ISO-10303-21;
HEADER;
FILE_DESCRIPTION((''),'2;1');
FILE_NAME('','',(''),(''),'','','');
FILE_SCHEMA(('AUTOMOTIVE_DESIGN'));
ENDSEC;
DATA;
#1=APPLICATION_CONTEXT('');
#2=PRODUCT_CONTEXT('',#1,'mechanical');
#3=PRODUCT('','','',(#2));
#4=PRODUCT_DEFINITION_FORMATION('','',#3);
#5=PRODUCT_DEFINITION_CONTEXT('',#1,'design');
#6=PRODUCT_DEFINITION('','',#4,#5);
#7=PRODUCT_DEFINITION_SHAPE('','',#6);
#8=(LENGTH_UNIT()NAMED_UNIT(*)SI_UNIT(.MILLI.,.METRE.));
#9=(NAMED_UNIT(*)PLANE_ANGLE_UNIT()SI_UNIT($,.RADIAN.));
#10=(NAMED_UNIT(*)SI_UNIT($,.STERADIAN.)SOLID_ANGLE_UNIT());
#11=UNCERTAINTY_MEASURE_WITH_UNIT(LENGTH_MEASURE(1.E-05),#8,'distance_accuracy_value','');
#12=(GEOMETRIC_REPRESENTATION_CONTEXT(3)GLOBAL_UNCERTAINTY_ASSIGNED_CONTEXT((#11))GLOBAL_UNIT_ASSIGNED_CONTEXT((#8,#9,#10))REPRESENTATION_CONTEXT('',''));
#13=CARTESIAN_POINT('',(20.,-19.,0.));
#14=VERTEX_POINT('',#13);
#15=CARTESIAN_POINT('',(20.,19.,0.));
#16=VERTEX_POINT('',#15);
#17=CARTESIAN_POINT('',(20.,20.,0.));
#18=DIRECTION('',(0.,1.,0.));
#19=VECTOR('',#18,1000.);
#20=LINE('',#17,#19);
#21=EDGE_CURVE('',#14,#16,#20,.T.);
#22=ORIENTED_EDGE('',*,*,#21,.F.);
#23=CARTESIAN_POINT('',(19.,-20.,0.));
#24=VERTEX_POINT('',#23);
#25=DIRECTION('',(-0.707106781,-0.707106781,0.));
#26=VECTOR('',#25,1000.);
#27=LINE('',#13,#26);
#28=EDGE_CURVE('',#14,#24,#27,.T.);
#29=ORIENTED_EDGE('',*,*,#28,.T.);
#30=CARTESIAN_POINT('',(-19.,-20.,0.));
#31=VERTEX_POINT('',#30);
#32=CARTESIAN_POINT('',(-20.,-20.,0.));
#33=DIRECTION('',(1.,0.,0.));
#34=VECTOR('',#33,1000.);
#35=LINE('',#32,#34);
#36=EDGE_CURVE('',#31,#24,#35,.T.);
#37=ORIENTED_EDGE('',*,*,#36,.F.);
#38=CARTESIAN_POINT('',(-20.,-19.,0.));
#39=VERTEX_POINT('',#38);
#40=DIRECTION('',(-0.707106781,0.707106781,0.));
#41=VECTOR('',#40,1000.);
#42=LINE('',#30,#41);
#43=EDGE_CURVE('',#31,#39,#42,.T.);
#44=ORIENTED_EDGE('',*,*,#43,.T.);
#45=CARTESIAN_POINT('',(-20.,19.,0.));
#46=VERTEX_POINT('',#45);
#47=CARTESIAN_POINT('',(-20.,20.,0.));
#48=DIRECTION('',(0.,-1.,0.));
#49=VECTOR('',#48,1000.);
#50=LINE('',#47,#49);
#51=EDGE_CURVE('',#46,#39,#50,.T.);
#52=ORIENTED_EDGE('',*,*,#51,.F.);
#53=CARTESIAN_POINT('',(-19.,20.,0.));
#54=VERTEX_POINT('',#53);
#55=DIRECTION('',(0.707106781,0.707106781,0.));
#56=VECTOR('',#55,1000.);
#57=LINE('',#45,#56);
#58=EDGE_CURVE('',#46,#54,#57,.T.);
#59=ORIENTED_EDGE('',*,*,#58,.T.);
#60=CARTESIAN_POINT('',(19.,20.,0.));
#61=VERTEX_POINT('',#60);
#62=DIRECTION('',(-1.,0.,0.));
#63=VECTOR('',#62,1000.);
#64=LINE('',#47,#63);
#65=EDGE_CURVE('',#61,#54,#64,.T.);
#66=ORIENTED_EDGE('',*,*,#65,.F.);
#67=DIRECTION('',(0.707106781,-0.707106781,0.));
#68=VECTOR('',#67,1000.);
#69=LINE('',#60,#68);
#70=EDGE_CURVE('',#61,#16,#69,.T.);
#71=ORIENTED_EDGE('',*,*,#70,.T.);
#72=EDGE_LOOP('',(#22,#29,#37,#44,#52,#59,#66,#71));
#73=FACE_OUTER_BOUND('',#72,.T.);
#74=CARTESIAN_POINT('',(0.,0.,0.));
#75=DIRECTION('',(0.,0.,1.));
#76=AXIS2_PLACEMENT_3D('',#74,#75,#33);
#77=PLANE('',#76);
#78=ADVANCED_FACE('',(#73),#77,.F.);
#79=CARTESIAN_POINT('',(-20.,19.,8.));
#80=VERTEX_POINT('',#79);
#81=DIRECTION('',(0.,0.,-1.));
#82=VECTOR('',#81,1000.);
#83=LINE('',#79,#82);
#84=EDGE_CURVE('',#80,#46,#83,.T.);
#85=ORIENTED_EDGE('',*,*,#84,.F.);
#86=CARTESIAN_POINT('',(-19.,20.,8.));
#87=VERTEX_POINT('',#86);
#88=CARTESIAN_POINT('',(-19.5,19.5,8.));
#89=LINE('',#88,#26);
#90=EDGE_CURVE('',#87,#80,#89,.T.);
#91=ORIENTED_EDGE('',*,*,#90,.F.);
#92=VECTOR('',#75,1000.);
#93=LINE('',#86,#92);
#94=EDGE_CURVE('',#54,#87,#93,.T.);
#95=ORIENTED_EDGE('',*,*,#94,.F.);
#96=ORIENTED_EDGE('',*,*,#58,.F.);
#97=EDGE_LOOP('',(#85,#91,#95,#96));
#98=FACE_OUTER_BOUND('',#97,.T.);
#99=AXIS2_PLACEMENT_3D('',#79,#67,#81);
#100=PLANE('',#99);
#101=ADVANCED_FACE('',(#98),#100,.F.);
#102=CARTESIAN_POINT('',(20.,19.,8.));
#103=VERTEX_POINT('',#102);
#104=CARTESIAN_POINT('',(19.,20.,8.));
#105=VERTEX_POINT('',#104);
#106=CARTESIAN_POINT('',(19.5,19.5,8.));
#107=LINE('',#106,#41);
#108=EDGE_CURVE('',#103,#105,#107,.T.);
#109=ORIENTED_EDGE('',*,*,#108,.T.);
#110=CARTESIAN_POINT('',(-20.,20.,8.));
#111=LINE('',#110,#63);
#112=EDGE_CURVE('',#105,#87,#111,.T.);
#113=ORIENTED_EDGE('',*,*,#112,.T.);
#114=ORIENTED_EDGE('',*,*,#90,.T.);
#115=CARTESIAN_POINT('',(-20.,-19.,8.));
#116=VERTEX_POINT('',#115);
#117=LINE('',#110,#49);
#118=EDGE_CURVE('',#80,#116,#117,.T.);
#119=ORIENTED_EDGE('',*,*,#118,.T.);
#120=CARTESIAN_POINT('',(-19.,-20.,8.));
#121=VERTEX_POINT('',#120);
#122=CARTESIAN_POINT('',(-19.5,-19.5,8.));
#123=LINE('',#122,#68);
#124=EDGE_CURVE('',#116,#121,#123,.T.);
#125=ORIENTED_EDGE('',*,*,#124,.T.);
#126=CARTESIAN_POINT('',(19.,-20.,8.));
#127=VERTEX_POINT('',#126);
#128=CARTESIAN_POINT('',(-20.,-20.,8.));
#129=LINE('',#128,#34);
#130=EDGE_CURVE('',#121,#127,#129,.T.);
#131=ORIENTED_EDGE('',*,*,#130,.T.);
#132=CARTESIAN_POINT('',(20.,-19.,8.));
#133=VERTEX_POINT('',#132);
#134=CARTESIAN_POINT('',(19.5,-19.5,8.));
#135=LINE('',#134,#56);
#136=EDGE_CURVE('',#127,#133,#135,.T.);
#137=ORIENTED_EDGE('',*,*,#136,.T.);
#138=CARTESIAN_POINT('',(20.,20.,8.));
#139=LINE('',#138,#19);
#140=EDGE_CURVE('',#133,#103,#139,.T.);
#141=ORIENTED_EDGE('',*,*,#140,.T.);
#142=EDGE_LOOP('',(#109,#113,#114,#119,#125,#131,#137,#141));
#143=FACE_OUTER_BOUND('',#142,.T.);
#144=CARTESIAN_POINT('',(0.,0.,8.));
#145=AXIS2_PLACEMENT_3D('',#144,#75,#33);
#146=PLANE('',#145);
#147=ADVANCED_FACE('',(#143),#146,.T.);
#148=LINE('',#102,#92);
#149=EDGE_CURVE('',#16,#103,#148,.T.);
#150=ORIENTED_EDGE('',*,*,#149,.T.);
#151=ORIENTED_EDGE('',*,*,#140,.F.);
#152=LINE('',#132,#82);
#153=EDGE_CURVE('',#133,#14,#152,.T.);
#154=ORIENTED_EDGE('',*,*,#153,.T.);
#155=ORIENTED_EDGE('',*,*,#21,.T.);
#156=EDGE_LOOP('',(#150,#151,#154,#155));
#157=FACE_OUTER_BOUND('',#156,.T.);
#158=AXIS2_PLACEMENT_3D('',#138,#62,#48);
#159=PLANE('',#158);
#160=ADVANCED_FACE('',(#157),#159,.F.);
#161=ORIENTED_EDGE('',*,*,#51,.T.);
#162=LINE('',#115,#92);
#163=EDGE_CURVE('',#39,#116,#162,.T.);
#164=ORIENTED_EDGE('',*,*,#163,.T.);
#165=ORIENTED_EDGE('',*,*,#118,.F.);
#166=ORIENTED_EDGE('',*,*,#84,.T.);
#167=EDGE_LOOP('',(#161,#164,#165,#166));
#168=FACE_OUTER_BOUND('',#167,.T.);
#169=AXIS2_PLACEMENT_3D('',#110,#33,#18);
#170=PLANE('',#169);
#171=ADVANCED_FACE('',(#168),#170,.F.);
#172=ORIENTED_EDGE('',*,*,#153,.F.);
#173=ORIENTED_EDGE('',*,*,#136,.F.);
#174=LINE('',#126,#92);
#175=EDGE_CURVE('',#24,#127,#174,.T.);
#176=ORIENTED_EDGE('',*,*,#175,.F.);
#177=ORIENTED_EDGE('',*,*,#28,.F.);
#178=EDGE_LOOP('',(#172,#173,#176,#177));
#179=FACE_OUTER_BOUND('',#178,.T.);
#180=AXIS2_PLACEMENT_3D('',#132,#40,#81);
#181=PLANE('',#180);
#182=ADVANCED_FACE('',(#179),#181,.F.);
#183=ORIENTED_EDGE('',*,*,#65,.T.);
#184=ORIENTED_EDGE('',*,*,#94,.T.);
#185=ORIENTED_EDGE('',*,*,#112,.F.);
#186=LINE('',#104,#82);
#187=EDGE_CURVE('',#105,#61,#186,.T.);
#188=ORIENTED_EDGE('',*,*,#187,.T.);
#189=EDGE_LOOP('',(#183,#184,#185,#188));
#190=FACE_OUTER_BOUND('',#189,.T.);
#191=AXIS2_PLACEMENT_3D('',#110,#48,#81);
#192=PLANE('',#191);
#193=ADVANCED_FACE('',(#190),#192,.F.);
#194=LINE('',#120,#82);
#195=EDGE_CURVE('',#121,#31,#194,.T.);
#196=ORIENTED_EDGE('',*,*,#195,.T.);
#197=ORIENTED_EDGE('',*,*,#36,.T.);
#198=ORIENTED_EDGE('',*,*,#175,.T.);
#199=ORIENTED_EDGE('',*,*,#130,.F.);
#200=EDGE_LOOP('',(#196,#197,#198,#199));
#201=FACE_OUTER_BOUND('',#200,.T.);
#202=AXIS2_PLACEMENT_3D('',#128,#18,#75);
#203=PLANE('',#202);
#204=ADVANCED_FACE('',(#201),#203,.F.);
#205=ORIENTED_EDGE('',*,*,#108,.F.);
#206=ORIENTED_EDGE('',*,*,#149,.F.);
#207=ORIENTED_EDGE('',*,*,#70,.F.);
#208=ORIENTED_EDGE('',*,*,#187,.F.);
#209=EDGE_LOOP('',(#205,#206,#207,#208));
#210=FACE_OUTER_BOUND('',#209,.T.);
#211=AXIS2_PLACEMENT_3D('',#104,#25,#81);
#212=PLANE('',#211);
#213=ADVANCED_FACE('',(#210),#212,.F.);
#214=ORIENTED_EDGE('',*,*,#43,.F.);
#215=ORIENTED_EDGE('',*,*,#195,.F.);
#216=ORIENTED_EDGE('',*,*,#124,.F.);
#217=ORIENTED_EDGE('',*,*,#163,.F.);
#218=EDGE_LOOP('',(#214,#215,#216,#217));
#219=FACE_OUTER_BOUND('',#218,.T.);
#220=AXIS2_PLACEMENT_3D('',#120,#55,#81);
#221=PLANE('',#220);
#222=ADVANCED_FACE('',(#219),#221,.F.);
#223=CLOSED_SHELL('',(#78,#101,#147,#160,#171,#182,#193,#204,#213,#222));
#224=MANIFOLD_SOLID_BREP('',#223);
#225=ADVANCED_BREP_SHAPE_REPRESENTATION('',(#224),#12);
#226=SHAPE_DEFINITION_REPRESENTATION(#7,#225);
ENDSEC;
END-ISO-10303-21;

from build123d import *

# Parameters (mm, degrees)
SKETCH1_W           = 40
SKETCH1_H           = 40
BOSS_EXTRUDE1_DEPTH = 8
CHAMFER1_SIZE       = 1


with BuildPart() as part:
    # Sketch1 → Boss-Extrude1 (new body)
    with BuildSketch(Plane.XY):
        Rectangle(SKETCH1_W, SKETCH1_H)
    extrude(amount=BOSS_EXTRUDE1_DEPTH)

    # Chamfer1
    chamfer1_edges = [part.edges().sort_by_distance(p)[0] for p in [
        (20, -20, 4),
        (-20, -20, 4),
        (-20, 20, 4),
        (20, 20, 4),
    ]]
    chamfer(chamfer1_edges, length=CHAMFER1_SIZE)


solid = part.part
